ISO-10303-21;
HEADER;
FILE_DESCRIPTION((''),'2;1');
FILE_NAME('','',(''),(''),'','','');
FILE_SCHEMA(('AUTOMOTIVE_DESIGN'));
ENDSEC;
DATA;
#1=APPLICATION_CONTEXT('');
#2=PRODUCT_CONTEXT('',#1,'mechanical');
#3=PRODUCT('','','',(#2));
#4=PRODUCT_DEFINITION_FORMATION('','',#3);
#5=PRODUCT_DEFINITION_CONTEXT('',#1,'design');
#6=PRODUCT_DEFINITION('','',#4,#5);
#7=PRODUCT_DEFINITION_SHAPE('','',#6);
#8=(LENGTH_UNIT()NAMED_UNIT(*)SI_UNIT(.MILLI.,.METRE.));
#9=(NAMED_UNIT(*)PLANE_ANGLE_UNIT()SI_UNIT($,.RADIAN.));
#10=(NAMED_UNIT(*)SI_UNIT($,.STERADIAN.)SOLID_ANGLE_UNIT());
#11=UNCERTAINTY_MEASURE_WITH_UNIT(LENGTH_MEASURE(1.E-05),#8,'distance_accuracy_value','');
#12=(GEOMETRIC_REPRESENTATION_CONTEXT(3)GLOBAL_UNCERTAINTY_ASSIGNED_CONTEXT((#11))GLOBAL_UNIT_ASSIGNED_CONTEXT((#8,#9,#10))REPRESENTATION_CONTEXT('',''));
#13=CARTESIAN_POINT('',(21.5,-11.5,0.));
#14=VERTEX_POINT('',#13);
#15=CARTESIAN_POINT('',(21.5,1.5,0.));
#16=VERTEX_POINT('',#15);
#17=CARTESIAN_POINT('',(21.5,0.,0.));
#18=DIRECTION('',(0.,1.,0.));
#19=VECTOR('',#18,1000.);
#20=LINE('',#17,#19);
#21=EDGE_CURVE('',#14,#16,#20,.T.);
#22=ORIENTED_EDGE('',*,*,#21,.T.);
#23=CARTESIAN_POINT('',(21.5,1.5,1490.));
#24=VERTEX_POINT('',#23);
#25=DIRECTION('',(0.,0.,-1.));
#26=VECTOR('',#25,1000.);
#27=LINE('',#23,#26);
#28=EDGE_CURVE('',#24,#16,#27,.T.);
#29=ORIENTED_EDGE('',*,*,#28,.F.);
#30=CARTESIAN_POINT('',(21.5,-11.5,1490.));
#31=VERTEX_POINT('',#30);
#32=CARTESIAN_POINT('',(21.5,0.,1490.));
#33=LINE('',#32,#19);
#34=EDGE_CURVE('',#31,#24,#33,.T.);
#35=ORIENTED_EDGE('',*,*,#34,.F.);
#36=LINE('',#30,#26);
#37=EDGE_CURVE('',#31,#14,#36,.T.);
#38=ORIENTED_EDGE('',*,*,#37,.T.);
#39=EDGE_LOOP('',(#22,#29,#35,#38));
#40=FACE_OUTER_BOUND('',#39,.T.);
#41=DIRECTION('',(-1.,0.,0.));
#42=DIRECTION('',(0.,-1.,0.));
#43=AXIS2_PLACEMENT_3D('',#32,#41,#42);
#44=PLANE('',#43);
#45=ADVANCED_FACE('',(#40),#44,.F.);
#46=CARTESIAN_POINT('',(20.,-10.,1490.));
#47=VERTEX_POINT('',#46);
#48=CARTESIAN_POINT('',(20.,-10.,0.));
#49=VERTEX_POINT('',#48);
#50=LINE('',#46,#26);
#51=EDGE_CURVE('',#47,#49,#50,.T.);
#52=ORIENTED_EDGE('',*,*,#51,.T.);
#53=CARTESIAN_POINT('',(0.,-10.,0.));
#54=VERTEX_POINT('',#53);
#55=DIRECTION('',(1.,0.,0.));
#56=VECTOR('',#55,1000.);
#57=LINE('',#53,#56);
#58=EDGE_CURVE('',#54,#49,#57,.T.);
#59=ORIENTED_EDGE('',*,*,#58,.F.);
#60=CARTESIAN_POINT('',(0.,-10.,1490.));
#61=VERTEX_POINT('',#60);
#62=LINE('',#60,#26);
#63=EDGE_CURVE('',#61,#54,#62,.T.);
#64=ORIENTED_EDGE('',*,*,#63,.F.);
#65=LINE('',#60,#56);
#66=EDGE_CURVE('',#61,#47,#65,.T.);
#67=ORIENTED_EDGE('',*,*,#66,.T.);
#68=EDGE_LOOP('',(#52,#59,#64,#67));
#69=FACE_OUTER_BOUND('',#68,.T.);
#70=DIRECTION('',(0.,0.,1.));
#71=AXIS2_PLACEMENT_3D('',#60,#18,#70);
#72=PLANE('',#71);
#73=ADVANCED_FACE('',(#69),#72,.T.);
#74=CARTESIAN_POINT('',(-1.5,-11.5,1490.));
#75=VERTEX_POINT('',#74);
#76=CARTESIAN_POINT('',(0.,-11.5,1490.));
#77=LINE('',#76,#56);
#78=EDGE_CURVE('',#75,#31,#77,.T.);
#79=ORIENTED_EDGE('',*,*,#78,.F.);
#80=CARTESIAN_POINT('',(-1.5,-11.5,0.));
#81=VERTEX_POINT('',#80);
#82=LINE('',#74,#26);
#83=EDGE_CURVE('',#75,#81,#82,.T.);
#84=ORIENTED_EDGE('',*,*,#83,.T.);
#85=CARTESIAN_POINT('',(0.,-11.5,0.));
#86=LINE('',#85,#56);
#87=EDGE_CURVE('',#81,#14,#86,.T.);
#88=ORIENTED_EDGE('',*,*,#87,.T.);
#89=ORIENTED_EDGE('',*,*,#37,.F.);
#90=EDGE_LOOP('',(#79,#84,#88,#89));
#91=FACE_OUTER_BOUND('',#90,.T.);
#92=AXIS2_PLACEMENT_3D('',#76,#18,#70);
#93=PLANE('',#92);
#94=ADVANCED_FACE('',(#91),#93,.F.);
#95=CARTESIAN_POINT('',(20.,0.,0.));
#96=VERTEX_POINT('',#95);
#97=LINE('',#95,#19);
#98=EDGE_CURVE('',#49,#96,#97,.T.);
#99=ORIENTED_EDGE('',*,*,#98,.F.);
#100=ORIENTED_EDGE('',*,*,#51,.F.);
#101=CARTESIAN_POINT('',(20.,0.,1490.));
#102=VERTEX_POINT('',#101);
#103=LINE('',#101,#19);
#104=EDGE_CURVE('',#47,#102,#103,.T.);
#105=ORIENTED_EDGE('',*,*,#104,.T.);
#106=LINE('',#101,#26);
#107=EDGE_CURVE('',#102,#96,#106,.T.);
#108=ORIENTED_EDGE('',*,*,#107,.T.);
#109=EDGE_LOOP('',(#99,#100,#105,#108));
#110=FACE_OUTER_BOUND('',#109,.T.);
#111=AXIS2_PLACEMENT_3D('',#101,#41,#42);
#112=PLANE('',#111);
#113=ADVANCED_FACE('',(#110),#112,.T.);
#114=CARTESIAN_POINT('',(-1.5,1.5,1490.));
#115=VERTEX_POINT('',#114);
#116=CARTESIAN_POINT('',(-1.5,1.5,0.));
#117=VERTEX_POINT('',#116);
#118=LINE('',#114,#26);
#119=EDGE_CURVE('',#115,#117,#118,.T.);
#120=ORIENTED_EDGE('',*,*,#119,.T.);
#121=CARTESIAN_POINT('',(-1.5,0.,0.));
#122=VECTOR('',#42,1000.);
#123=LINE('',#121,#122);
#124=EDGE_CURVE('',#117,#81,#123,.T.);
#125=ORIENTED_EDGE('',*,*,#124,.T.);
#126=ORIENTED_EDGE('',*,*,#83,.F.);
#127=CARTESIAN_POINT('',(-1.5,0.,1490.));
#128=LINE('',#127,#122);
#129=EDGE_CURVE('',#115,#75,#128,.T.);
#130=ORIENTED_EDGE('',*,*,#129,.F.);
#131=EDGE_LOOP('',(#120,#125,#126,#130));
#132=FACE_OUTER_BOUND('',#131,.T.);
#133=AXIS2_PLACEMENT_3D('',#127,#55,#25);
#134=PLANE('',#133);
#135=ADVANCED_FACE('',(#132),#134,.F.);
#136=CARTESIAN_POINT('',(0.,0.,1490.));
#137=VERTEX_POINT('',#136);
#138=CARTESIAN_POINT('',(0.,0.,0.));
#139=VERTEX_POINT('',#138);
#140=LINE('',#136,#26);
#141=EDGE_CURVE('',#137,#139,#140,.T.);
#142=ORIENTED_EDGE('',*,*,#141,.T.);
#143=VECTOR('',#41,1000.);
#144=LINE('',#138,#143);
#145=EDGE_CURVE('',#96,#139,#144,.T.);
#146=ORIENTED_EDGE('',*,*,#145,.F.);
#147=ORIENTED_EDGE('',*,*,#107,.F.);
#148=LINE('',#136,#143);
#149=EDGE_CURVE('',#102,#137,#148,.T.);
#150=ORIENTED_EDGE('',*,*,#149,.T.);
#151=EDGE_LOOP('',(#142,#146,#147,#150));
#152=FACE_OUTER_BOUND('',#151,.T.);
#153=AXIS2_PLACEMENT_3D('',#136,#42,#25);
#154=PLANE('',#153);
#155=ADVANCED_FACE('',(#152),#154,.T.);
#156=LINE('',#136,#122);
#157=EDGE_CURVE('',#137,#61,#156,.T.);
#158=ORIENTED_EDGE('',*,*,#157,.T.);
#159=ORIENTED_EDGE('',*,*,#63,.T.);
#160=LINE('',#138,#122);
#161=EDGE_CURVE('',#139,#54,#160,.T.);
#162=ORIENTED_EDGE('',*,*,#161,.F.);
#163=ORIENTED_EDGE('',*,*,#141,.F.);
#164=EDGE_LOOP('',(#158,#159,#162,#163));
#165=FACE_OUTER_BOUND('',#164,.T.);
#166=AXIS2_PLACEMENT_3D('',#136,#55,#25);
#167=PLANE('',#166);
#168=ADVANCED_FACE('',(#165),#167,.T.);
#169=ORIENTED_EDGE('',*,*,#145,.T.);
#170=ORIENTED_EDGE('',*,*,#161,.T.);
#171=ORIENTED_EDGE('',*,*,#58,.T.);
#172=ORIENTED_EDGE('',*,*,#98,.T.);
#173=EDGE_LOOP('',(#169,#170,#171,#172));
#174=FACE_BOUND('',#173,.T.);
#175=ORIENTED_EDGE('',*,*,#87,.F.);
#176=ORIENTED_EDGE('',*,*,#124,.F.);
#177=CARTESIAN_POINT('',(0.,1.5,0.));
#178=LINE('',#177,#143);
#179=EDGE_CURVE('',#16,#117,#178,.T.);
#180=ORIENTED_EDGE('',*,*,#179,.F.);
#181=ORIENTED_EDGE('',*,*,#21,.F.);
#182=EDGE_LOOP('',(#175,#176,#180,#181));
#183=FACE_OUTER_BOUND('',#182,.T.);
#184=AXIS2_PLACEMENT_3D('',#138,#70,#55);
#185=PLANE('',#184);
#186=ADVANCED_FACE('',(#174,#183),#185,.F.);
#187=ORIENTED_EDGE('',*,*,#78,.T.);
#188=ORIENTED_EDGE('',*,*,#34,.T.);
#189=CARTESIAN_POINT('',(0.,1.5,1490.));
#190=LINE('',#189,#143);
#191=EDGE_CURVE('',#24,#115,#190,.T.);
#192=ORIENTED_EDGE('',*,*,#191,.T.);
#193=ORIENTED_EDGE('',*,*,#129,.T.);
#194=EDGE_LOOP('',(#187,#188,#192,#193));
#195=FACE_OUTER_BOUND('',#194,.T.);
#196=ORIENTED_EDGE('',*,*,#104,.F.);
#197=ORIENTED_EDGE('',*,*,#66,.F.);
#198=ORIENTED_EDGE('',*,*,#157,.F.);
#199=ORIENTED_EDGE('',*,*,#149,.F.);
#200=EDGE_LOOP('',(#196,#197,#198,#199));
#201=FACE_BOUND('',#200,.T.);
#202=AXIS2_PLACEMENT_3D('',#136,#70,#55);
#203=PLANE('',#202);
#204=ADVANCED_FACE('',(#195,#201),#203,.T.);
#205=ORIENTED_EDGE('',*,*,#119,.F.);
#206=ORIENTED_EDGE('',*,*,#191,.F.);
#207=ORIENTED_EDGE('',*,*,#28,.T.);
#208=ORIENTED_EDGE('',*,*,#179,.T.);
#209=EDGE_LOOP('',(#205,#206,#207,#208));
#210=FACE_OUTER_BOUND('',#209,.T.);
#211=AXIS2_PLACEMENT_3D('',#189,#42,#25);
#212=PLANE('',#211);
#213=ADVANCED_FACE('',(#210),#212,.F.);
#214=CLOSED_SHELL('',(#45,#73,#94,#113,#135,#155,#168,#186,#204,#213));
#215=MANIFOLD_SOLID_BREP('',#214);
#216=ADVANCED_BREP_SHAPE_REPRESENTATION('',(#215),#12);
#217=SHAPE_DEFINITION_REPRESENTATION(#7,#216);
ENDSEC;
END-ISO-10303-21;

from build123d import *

# Parameters (mm, degrees)
SKETCH1_W           = 23
SKETCH1_H           = 13
SKETCH1_W_2         = 20
SKETCH1_H_2         = 10
EXTRUDE_THIN1_DEPTH = 1490


with BuildPart() as part:
    # Sketch1 → Extrude-Thin1 (new body)
    with BuildSketch(Plane.XY):
        with Locations((10, -5)):
            Rectangle(SKETCH1_W, SKETCH1_H)
        with Locations((10, -5)):
            Rectangle(SKETCH1_W_2, SKETCH1_H_2, mode=Mode.SUBTRACT)
    extrude(amount=EXTRUDE_THIN1_DEPTH)


solid = part.part
